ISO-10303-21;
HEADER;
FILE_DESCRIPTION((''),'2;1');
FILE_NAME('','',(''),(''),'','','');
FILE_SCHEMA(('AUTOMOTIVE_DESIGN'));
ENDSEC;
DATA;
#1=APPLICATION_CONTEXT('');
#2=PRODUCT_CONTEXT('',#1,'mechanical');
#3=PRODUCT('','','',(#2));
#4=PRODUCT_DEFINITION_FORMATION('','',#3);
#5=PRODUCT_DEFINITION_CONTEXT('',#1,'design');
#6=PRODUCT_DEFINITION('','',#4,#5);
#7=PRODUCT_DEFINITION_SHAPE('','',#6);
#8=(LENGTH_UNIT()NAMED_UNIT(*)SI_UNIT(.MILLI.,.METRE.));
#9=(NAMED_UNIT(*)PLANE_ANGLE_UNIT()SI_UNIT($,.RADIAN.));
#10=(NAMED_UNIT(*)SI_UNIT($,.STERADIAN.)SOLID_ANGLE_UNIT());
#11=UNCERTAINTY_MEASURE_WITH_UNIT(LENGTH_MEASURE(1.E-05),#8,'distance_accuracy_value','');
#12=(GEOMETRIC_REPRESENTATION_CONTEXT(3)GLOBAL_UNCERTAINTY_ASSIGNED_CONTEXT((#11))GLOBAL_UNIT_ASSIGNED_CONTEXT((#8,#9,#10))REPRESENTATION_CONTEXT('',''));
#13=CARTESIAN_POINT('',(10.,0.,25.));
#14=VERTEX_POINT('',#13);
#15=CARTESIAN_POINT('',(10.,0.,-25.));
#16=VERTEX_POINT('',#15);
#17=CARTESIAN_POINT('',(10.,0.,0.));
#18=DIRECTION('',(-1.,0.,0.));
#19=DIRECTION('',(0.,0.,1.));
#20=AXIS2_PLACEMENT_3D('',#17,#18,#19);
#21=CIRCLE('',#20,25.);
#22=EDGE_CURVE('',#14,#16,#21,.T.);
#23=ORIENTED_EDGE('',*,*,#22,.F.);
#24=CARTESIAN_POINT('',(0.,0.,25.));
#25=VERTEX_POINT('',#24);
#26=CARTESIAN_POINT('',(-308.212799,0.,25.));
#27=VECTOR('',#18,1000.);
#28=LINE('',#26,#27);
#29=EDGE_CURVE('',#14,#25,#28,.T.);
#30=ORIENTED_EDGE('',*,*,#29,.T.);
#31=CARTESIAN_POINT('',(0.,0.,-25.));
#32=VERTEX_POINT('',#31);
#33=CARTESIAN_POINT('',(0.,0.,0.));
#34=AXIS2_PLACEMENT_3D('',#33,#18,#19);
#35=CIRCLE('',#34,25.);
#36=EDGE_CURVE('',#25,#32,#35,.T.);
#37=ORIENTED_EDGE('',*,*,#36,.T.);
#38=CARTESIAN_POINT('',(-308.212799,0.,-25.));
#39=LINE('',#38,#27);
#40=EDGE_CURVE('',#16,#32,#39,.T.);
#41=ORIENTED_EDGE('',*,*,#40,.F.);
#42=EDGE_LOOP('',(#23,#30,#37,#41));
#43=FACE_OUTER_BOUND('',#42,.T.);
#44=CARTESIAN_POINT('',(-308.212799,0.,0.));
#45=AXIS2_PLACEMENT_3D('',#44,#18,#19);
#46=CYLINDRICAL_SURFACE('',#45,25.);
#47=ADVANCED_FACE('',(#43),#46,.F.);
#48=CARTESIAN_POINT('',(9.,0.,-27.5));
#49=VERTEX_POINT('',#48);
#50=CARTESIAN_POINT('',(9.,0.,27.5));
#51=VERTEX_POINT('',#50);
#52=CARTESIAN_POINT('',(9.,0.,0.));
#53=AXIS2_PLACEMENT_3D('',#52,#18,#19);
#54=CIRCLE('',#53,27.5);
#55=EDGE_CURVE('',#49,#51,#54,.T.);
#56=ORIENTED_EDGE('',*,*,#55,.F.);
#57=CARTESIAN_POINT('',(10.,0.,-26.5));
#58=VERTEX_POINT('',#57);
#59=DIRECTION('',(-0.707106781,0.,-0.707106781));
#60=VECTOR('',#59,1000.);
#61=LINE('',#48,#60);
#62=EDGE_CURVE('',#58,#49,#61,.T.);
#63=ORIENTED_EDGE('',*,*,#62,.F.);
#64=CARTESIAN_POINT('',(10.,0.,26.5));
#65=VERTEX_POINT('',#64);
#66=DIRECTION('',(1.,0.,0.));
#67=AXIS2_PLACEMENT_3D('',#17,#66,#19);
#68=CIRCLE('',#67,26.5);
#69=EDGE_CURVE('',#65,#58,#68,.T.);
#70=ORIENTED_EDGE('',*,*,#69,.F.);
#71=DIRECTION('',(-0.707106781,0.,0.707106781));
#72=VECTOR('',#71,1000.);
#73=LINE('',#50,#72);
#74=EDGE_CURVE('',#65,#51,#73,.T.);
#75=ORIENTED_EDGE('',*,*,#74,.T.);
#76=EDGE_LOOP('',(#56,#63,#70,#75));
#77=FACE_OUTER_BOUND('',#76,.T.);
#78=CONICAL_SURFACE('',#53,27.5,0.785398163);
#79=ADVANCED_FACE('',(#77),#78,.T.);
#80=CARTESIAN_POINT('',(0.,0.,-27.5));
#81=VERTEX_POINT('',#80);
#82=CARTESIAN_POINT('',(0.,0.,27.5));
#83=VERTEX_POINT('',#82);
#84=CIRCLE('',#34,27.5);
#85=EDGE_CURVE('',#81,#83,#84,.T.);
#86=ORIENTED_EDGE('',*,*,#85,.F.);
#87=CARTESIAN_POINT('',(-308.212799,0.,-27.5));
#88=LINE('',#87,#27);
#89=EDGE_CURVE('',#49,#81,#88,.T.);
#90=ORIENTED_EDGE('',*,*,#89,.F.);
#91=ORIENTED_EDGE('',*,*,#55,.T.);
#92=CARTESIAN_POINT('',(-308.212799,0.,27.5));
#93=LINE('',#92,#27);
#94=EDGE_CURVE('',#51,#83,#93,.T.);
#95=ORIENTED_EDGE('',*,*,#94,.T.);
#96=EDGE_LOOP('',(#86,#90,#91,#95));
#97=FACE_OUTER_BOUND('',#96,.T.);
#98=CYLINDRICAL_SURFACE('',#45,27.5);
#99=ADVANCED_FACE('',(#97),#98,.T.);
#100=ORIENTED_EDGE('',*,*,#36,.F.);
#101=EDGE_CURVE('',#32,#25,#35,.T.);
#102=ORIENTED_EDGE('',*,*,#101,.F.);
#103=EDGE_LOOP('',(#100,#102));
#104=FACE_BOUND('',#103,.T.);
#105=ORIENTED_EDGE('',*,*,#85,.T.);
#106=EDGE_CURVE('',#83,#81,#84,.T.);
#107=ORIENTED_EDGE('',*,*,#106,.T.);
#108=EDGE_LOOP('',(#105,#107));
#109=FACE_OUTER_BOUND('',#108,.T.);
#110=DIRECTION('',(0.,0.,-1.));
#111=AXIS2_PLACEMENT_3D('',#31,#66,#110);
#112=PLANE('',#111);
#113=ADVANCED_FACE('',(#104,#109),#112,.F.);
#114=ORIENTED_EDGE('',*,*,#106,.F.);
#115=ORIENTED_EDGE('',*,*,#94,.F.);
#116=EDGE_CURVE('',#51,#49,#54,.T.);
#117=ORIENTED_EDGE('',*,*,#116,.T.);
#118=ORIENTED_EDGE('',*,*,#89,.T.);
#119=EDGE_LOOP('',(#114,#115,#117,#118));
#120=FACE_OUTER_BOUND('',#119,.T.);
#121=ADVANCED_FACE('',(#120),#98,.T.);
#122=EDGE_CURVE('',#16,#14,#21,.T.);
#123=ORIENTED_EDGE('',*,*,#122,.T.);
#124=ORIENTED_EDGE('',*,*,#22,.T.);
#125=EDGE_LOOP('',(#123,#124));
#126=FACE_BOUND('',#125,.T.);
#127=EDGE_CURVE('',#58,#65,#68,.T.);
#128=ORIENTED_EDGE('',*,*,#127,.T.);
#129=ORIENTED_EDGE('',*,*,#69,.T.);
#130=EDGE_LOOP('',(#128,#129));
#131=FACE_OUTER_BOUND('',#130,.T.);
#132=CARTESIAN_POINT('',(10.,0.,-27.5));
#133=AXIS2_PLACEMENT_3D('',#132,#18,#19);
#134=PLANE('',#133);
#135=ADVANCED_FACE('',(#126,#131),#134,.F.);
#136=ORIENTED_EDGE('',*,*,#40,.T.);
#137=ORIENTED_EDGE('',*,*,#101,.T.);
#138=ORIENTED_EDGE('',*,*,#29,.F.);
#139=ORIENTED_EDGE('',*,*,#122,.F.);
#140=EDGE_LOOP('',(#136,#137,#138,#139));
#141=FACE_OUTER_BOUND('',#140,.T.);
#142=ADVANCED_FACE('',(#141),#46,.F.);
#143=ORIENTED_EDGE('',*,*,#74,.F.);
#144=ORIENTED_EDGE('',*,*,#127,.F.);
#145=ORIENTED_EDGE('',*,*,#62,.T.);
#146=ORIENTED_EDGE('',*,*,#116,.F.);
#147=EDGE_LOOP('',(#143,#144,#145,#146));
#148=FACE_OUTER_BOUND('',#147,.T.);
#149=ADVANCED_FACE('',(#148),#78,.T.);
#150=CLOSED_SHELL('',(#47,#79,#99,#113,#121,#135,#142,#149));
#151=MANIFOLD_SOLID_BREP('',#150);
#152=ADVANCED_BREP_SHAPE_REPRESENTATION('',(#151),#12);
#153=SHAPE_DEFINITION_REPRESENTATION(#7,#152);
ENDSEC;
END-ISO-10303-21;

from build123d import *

# Parameters (mm, degrees)
SKETCH_1_W     = 10
SKETCH_1_H     = 2.5
CHAMFER_1_SIZE = 1


with BuildPart() as part:
    # 草图1 → 旋转1 (revolve)
    with BuildSketch(Plane(origin=(0, 0, 0), x_dir=(1, 0, 0), z_dir=(0, 1, 0)), mode=Mode.PRIVATE) as revolve_1_sk:
        with Locations((5, 26.25)):
            Rectangle(SKETCH_1_W, SKETCH_1_H)
    revolve(revolve_1_sk.sketch.rotate(Axis((-308.212798969, 0, 0), (1, 0, 0)), 180), axis=Axis((-308.212798969, 0, 0), (1, 0, 0)))

    # 倒角1
    chamfer_1_edges = [part.edges().sort_by_distance(p)[0] for p in [
        (10, 0, -27.5),
    ]]
    chamfer(chamfer_1_edges, length=CHAMFER_1_SIZE)


solid = part.part
